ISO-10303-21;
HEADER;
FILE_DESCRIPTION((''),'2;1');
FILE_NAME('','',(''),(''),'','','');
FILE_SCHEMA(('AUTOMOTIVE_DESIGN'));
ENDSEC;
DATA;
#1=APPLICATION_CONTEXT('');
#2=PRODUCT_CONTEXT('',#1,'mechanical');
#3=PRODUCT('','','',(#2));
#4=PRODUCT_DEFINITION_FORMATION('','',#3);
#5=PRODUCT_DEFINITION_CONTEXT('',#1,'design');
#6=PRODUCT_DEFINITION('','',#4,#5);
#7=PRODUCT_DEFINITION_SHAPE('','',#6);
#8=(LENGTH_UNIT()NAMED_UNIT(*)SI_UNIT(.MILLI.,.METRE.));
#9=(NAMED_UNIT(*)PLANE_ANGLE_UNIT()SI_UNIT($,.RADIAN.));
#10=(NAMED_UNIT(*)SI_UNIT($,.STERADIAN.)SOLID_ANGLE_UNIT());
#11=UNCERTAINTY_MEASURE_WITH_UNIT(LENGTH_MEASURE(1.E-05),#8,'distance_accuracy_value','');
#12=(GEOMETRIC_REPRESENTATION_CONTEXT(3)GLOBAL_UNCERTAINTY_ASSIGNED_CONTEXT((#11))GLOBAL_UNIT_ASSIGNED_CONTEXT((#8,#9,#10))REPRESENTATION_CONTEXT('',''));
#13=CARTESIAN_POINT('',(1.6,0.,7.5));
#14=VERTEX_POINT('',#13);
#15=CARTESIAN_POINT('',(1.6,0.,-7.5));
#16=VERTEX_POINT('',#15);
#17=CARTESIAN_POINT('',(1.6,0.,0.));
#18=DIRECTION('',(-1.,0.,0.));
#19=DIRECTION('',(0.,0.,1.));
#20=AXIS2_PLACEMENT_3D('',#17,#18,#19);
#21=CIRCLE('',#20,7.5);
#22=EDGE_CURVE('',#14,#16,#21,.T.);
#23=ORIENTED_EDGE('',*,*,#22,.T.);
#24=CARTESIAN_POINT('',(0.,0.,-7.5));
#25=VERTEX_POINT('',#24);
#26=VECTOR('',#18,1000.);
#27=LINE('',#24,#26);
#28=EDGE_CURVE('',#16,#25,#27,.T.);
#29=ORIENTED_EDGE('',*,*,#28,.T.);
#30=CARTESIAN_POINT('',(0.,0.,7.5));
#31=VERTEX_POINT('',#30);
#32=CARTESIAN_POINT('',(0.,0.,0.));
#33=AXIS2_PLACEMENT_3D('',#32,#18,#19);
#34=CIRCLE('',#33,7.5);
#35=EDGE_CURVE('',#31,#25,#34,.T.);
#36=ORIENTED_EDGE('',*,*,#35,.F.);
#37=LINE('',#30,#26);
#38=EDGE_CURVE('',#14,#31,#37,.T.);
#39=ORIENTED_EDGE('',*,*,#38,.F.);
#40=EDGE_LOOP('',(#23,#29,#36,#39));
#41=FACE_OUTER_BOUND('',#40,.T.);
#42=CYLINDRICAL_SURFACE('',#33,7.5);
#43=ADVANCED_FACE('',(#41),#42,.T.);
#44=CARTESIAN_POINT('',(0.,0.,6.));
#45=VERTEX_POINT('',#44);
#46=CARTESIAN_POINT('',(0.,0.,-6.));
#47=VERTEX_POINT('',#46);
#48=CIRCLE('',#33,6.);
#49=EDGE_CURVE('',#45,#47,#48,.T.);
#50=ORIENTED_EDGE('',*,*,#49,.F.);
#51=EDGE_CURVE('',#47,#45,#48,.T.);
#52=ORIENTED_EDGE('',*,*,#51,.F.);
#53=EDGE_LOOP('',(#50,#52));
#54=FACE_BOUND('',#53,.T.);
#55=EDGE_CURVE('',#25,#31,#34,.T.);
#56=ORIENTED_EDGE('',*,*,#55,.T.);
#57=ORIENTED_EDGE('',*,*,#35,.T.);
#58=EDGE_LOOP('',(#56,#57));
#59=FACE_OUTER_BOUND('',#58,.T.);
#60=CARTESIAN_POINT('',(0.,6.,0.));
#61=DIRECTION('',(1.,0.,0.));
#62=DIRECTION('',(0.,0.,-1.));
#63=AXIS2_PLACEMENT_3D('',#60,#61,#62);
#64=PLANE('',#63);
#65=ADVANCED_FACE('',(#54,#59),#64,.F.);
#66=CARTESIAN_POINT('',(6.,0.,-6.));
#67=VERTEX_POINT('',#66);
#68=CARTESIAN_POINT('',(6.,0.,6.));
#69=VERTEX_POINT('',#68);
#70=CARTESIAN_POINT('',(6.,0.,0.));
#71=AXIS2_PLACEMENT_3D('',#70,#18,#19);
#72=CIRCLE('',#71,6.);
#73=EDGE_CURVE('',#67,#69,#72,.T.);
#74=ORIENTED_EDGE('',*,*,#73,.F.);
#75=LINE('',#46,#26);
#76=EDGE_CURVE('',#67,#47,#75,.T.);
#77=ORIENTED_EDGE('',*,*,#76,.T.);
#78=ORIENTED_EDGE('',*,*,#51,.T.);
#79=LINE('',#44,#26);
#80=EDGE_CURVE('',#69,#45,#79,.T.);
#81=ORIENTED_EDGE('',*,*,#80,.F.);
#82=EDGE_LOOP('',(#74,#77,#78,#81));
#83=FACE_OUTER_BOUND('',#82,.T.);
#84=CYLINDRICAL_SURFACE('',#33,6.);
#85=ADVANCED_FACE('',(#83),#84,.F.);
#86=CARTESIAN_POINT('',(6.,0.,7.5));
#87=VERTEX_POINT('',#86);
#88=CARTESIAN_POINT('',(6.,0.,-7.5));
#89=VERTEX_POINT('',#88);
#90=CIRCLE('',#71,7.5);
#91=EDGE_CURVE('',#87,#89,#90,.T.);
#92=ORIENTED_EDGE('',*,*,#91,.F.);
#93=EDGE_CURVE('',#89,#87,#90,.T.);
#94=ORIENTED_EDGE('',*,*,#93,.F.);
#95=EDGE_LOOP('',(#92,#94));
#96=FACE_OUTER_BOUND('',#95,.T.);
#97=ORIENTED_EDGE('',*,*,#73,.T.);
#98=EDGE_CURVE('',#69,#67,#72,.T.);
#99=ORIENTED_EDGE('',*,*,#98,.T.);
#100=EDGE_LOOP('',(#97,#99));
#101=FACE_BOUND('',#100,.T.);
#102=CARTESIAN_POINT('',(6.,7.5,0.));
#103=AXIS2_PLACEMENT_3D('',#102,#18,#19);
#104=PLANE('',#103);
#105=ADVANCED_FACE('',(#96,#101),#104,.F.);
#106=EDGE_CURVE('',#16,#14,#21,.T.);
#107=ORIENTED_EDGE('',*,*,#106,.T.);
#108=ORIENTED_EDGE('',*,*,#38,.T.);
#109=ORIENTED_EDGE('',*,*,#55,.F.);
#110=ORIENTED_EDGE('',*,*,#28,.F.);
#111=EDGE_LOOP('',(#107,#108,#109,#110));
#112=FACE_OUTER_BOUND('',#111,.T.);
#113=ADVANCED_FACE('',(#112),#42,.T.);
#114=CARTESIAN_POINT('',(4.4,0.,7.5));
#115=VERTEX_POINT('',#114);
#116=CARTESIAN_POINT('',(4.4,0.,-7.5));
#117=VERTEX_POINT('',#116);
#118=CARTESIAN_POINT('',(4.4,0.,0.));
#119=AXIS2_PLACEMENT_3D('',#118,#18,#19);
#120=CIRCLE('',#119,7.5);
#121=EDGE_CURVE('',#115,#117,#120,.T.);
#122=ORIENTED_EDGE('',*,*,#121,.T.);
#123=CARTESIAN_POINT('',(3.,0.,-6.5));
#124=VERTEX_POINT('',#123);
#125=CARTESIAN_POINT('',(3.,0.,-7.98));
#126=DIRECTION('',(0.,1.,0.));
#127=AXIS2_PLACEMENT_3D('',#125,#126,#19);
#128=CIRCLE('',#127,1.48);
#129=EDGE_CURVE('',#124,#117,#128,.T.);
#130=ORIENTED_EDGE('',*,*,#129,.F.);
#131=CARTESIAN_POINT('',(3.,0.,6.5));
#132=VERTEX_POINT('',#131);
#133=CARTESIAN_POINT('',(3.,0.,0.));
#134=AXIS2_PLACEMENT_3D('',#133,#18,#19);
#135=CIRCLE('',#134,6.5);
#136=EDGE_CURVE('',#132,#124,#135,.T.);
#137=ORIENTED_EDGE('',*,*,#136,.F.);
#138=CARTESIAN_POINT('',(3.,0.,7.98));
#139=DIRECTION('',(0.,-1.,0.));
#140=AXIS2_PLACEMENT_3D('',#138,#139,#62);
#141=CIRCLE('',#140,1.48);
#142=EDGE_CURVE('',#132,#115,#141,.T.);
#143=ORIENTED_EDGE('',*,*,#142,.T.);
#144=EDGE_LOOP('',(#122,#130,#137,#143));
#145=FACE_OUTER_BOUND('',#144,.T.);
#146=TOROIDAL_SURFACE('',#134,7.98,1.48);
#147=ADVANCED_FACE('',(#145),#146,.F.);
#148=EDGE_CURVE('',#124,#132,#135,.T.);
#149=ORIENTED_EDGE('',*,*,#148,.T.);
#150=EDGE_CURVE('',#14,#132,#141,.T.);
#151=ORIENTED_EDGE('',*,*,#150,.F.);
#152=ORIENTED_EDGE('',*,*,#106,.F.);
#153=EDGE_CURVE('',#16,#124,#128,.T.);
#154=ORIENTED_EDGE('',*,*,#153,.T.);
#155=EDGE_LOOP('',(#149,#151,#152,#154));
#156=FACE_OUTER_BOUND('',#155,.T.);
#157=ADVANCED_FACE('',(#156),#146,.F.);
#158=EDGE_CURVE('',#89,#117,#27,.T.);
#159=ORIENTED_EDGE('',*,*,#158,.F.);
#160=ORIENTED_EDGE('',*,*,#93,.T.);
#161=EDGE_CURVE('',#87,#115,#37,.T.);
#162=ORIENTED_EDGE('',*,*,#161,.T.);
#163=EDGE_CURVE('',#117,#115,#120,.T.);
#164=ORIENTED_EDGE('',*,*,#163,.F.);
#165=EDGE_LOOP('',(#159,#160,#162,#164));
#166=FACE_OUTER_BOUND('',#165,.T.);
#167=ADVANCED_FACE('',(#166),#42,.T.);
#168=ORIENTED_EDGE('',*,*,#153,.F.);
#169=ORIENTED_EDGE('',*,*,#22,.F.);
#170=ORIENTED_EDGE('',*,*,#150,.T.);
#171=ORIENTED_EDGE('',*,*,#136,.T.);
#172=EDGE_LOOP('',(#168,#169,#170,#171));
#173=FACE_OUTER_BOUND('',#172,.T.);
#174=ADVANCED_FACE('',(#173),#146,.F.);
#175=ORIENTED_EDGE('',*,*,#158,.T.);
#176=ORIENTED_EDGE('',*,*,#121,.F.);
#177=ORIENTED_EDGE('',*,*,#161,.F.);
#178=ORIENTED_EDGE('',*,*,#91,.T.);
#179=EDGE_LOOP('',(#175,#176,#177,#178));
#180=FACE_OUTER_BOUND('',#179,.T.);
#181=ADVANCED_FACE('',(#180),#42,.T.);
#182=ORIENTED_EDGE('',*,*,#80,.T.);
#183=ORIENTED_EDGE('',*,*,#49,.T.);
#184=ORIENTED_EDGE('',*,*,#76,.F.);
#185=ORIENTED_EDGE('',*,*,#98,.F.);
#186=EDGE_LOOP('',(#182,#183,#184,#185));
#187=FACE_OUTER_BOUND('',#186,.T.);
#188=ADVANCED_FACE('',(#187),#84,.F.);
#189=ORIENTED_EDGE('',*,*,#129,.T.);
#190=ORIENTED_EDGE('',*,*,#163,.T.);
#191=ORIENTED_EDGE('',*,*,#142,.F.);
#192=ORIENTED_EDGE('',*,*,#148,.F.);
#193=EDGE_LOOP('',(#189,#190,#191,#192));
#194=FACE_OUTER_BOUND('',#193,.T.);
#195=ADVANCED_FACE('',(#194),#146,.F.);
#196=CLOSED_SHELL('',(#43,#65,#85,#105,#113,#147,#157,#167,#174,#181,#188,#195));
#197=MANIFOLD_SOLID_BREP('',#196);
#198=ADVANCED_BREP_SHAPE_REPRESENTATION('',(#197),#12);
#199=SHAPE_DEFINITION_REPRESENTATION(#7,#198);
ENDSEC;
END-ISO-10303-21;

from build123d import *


with BuildPart() as part:
    # Sketch1 → Revolve1 (revolve)
    with BuildSketch(Plane.XY, mode=Mode.PRIVATE) as revolve1_sk:
        with BuildLine():
            Line((0, 6), (0, 7.5))
            Line((0, 7.5), (1.6, 7.5))
            ThreePointArc((1.6, 7.5), (3, 6.5), (4.4, 7.5))
            Line((4.4, 7.5), (6, 7.5))
            Line((6, 7.5), (6, 6))
            Line((6, 6), (0, 6))
        make_face()
    revolve(revolve1_sk.sketch.rotate(Axis((0, 0, 0), (1, 0, 0)), 90), axis=Axis((0, 0, 0), (1, 0, 0)))


solid = part.part
